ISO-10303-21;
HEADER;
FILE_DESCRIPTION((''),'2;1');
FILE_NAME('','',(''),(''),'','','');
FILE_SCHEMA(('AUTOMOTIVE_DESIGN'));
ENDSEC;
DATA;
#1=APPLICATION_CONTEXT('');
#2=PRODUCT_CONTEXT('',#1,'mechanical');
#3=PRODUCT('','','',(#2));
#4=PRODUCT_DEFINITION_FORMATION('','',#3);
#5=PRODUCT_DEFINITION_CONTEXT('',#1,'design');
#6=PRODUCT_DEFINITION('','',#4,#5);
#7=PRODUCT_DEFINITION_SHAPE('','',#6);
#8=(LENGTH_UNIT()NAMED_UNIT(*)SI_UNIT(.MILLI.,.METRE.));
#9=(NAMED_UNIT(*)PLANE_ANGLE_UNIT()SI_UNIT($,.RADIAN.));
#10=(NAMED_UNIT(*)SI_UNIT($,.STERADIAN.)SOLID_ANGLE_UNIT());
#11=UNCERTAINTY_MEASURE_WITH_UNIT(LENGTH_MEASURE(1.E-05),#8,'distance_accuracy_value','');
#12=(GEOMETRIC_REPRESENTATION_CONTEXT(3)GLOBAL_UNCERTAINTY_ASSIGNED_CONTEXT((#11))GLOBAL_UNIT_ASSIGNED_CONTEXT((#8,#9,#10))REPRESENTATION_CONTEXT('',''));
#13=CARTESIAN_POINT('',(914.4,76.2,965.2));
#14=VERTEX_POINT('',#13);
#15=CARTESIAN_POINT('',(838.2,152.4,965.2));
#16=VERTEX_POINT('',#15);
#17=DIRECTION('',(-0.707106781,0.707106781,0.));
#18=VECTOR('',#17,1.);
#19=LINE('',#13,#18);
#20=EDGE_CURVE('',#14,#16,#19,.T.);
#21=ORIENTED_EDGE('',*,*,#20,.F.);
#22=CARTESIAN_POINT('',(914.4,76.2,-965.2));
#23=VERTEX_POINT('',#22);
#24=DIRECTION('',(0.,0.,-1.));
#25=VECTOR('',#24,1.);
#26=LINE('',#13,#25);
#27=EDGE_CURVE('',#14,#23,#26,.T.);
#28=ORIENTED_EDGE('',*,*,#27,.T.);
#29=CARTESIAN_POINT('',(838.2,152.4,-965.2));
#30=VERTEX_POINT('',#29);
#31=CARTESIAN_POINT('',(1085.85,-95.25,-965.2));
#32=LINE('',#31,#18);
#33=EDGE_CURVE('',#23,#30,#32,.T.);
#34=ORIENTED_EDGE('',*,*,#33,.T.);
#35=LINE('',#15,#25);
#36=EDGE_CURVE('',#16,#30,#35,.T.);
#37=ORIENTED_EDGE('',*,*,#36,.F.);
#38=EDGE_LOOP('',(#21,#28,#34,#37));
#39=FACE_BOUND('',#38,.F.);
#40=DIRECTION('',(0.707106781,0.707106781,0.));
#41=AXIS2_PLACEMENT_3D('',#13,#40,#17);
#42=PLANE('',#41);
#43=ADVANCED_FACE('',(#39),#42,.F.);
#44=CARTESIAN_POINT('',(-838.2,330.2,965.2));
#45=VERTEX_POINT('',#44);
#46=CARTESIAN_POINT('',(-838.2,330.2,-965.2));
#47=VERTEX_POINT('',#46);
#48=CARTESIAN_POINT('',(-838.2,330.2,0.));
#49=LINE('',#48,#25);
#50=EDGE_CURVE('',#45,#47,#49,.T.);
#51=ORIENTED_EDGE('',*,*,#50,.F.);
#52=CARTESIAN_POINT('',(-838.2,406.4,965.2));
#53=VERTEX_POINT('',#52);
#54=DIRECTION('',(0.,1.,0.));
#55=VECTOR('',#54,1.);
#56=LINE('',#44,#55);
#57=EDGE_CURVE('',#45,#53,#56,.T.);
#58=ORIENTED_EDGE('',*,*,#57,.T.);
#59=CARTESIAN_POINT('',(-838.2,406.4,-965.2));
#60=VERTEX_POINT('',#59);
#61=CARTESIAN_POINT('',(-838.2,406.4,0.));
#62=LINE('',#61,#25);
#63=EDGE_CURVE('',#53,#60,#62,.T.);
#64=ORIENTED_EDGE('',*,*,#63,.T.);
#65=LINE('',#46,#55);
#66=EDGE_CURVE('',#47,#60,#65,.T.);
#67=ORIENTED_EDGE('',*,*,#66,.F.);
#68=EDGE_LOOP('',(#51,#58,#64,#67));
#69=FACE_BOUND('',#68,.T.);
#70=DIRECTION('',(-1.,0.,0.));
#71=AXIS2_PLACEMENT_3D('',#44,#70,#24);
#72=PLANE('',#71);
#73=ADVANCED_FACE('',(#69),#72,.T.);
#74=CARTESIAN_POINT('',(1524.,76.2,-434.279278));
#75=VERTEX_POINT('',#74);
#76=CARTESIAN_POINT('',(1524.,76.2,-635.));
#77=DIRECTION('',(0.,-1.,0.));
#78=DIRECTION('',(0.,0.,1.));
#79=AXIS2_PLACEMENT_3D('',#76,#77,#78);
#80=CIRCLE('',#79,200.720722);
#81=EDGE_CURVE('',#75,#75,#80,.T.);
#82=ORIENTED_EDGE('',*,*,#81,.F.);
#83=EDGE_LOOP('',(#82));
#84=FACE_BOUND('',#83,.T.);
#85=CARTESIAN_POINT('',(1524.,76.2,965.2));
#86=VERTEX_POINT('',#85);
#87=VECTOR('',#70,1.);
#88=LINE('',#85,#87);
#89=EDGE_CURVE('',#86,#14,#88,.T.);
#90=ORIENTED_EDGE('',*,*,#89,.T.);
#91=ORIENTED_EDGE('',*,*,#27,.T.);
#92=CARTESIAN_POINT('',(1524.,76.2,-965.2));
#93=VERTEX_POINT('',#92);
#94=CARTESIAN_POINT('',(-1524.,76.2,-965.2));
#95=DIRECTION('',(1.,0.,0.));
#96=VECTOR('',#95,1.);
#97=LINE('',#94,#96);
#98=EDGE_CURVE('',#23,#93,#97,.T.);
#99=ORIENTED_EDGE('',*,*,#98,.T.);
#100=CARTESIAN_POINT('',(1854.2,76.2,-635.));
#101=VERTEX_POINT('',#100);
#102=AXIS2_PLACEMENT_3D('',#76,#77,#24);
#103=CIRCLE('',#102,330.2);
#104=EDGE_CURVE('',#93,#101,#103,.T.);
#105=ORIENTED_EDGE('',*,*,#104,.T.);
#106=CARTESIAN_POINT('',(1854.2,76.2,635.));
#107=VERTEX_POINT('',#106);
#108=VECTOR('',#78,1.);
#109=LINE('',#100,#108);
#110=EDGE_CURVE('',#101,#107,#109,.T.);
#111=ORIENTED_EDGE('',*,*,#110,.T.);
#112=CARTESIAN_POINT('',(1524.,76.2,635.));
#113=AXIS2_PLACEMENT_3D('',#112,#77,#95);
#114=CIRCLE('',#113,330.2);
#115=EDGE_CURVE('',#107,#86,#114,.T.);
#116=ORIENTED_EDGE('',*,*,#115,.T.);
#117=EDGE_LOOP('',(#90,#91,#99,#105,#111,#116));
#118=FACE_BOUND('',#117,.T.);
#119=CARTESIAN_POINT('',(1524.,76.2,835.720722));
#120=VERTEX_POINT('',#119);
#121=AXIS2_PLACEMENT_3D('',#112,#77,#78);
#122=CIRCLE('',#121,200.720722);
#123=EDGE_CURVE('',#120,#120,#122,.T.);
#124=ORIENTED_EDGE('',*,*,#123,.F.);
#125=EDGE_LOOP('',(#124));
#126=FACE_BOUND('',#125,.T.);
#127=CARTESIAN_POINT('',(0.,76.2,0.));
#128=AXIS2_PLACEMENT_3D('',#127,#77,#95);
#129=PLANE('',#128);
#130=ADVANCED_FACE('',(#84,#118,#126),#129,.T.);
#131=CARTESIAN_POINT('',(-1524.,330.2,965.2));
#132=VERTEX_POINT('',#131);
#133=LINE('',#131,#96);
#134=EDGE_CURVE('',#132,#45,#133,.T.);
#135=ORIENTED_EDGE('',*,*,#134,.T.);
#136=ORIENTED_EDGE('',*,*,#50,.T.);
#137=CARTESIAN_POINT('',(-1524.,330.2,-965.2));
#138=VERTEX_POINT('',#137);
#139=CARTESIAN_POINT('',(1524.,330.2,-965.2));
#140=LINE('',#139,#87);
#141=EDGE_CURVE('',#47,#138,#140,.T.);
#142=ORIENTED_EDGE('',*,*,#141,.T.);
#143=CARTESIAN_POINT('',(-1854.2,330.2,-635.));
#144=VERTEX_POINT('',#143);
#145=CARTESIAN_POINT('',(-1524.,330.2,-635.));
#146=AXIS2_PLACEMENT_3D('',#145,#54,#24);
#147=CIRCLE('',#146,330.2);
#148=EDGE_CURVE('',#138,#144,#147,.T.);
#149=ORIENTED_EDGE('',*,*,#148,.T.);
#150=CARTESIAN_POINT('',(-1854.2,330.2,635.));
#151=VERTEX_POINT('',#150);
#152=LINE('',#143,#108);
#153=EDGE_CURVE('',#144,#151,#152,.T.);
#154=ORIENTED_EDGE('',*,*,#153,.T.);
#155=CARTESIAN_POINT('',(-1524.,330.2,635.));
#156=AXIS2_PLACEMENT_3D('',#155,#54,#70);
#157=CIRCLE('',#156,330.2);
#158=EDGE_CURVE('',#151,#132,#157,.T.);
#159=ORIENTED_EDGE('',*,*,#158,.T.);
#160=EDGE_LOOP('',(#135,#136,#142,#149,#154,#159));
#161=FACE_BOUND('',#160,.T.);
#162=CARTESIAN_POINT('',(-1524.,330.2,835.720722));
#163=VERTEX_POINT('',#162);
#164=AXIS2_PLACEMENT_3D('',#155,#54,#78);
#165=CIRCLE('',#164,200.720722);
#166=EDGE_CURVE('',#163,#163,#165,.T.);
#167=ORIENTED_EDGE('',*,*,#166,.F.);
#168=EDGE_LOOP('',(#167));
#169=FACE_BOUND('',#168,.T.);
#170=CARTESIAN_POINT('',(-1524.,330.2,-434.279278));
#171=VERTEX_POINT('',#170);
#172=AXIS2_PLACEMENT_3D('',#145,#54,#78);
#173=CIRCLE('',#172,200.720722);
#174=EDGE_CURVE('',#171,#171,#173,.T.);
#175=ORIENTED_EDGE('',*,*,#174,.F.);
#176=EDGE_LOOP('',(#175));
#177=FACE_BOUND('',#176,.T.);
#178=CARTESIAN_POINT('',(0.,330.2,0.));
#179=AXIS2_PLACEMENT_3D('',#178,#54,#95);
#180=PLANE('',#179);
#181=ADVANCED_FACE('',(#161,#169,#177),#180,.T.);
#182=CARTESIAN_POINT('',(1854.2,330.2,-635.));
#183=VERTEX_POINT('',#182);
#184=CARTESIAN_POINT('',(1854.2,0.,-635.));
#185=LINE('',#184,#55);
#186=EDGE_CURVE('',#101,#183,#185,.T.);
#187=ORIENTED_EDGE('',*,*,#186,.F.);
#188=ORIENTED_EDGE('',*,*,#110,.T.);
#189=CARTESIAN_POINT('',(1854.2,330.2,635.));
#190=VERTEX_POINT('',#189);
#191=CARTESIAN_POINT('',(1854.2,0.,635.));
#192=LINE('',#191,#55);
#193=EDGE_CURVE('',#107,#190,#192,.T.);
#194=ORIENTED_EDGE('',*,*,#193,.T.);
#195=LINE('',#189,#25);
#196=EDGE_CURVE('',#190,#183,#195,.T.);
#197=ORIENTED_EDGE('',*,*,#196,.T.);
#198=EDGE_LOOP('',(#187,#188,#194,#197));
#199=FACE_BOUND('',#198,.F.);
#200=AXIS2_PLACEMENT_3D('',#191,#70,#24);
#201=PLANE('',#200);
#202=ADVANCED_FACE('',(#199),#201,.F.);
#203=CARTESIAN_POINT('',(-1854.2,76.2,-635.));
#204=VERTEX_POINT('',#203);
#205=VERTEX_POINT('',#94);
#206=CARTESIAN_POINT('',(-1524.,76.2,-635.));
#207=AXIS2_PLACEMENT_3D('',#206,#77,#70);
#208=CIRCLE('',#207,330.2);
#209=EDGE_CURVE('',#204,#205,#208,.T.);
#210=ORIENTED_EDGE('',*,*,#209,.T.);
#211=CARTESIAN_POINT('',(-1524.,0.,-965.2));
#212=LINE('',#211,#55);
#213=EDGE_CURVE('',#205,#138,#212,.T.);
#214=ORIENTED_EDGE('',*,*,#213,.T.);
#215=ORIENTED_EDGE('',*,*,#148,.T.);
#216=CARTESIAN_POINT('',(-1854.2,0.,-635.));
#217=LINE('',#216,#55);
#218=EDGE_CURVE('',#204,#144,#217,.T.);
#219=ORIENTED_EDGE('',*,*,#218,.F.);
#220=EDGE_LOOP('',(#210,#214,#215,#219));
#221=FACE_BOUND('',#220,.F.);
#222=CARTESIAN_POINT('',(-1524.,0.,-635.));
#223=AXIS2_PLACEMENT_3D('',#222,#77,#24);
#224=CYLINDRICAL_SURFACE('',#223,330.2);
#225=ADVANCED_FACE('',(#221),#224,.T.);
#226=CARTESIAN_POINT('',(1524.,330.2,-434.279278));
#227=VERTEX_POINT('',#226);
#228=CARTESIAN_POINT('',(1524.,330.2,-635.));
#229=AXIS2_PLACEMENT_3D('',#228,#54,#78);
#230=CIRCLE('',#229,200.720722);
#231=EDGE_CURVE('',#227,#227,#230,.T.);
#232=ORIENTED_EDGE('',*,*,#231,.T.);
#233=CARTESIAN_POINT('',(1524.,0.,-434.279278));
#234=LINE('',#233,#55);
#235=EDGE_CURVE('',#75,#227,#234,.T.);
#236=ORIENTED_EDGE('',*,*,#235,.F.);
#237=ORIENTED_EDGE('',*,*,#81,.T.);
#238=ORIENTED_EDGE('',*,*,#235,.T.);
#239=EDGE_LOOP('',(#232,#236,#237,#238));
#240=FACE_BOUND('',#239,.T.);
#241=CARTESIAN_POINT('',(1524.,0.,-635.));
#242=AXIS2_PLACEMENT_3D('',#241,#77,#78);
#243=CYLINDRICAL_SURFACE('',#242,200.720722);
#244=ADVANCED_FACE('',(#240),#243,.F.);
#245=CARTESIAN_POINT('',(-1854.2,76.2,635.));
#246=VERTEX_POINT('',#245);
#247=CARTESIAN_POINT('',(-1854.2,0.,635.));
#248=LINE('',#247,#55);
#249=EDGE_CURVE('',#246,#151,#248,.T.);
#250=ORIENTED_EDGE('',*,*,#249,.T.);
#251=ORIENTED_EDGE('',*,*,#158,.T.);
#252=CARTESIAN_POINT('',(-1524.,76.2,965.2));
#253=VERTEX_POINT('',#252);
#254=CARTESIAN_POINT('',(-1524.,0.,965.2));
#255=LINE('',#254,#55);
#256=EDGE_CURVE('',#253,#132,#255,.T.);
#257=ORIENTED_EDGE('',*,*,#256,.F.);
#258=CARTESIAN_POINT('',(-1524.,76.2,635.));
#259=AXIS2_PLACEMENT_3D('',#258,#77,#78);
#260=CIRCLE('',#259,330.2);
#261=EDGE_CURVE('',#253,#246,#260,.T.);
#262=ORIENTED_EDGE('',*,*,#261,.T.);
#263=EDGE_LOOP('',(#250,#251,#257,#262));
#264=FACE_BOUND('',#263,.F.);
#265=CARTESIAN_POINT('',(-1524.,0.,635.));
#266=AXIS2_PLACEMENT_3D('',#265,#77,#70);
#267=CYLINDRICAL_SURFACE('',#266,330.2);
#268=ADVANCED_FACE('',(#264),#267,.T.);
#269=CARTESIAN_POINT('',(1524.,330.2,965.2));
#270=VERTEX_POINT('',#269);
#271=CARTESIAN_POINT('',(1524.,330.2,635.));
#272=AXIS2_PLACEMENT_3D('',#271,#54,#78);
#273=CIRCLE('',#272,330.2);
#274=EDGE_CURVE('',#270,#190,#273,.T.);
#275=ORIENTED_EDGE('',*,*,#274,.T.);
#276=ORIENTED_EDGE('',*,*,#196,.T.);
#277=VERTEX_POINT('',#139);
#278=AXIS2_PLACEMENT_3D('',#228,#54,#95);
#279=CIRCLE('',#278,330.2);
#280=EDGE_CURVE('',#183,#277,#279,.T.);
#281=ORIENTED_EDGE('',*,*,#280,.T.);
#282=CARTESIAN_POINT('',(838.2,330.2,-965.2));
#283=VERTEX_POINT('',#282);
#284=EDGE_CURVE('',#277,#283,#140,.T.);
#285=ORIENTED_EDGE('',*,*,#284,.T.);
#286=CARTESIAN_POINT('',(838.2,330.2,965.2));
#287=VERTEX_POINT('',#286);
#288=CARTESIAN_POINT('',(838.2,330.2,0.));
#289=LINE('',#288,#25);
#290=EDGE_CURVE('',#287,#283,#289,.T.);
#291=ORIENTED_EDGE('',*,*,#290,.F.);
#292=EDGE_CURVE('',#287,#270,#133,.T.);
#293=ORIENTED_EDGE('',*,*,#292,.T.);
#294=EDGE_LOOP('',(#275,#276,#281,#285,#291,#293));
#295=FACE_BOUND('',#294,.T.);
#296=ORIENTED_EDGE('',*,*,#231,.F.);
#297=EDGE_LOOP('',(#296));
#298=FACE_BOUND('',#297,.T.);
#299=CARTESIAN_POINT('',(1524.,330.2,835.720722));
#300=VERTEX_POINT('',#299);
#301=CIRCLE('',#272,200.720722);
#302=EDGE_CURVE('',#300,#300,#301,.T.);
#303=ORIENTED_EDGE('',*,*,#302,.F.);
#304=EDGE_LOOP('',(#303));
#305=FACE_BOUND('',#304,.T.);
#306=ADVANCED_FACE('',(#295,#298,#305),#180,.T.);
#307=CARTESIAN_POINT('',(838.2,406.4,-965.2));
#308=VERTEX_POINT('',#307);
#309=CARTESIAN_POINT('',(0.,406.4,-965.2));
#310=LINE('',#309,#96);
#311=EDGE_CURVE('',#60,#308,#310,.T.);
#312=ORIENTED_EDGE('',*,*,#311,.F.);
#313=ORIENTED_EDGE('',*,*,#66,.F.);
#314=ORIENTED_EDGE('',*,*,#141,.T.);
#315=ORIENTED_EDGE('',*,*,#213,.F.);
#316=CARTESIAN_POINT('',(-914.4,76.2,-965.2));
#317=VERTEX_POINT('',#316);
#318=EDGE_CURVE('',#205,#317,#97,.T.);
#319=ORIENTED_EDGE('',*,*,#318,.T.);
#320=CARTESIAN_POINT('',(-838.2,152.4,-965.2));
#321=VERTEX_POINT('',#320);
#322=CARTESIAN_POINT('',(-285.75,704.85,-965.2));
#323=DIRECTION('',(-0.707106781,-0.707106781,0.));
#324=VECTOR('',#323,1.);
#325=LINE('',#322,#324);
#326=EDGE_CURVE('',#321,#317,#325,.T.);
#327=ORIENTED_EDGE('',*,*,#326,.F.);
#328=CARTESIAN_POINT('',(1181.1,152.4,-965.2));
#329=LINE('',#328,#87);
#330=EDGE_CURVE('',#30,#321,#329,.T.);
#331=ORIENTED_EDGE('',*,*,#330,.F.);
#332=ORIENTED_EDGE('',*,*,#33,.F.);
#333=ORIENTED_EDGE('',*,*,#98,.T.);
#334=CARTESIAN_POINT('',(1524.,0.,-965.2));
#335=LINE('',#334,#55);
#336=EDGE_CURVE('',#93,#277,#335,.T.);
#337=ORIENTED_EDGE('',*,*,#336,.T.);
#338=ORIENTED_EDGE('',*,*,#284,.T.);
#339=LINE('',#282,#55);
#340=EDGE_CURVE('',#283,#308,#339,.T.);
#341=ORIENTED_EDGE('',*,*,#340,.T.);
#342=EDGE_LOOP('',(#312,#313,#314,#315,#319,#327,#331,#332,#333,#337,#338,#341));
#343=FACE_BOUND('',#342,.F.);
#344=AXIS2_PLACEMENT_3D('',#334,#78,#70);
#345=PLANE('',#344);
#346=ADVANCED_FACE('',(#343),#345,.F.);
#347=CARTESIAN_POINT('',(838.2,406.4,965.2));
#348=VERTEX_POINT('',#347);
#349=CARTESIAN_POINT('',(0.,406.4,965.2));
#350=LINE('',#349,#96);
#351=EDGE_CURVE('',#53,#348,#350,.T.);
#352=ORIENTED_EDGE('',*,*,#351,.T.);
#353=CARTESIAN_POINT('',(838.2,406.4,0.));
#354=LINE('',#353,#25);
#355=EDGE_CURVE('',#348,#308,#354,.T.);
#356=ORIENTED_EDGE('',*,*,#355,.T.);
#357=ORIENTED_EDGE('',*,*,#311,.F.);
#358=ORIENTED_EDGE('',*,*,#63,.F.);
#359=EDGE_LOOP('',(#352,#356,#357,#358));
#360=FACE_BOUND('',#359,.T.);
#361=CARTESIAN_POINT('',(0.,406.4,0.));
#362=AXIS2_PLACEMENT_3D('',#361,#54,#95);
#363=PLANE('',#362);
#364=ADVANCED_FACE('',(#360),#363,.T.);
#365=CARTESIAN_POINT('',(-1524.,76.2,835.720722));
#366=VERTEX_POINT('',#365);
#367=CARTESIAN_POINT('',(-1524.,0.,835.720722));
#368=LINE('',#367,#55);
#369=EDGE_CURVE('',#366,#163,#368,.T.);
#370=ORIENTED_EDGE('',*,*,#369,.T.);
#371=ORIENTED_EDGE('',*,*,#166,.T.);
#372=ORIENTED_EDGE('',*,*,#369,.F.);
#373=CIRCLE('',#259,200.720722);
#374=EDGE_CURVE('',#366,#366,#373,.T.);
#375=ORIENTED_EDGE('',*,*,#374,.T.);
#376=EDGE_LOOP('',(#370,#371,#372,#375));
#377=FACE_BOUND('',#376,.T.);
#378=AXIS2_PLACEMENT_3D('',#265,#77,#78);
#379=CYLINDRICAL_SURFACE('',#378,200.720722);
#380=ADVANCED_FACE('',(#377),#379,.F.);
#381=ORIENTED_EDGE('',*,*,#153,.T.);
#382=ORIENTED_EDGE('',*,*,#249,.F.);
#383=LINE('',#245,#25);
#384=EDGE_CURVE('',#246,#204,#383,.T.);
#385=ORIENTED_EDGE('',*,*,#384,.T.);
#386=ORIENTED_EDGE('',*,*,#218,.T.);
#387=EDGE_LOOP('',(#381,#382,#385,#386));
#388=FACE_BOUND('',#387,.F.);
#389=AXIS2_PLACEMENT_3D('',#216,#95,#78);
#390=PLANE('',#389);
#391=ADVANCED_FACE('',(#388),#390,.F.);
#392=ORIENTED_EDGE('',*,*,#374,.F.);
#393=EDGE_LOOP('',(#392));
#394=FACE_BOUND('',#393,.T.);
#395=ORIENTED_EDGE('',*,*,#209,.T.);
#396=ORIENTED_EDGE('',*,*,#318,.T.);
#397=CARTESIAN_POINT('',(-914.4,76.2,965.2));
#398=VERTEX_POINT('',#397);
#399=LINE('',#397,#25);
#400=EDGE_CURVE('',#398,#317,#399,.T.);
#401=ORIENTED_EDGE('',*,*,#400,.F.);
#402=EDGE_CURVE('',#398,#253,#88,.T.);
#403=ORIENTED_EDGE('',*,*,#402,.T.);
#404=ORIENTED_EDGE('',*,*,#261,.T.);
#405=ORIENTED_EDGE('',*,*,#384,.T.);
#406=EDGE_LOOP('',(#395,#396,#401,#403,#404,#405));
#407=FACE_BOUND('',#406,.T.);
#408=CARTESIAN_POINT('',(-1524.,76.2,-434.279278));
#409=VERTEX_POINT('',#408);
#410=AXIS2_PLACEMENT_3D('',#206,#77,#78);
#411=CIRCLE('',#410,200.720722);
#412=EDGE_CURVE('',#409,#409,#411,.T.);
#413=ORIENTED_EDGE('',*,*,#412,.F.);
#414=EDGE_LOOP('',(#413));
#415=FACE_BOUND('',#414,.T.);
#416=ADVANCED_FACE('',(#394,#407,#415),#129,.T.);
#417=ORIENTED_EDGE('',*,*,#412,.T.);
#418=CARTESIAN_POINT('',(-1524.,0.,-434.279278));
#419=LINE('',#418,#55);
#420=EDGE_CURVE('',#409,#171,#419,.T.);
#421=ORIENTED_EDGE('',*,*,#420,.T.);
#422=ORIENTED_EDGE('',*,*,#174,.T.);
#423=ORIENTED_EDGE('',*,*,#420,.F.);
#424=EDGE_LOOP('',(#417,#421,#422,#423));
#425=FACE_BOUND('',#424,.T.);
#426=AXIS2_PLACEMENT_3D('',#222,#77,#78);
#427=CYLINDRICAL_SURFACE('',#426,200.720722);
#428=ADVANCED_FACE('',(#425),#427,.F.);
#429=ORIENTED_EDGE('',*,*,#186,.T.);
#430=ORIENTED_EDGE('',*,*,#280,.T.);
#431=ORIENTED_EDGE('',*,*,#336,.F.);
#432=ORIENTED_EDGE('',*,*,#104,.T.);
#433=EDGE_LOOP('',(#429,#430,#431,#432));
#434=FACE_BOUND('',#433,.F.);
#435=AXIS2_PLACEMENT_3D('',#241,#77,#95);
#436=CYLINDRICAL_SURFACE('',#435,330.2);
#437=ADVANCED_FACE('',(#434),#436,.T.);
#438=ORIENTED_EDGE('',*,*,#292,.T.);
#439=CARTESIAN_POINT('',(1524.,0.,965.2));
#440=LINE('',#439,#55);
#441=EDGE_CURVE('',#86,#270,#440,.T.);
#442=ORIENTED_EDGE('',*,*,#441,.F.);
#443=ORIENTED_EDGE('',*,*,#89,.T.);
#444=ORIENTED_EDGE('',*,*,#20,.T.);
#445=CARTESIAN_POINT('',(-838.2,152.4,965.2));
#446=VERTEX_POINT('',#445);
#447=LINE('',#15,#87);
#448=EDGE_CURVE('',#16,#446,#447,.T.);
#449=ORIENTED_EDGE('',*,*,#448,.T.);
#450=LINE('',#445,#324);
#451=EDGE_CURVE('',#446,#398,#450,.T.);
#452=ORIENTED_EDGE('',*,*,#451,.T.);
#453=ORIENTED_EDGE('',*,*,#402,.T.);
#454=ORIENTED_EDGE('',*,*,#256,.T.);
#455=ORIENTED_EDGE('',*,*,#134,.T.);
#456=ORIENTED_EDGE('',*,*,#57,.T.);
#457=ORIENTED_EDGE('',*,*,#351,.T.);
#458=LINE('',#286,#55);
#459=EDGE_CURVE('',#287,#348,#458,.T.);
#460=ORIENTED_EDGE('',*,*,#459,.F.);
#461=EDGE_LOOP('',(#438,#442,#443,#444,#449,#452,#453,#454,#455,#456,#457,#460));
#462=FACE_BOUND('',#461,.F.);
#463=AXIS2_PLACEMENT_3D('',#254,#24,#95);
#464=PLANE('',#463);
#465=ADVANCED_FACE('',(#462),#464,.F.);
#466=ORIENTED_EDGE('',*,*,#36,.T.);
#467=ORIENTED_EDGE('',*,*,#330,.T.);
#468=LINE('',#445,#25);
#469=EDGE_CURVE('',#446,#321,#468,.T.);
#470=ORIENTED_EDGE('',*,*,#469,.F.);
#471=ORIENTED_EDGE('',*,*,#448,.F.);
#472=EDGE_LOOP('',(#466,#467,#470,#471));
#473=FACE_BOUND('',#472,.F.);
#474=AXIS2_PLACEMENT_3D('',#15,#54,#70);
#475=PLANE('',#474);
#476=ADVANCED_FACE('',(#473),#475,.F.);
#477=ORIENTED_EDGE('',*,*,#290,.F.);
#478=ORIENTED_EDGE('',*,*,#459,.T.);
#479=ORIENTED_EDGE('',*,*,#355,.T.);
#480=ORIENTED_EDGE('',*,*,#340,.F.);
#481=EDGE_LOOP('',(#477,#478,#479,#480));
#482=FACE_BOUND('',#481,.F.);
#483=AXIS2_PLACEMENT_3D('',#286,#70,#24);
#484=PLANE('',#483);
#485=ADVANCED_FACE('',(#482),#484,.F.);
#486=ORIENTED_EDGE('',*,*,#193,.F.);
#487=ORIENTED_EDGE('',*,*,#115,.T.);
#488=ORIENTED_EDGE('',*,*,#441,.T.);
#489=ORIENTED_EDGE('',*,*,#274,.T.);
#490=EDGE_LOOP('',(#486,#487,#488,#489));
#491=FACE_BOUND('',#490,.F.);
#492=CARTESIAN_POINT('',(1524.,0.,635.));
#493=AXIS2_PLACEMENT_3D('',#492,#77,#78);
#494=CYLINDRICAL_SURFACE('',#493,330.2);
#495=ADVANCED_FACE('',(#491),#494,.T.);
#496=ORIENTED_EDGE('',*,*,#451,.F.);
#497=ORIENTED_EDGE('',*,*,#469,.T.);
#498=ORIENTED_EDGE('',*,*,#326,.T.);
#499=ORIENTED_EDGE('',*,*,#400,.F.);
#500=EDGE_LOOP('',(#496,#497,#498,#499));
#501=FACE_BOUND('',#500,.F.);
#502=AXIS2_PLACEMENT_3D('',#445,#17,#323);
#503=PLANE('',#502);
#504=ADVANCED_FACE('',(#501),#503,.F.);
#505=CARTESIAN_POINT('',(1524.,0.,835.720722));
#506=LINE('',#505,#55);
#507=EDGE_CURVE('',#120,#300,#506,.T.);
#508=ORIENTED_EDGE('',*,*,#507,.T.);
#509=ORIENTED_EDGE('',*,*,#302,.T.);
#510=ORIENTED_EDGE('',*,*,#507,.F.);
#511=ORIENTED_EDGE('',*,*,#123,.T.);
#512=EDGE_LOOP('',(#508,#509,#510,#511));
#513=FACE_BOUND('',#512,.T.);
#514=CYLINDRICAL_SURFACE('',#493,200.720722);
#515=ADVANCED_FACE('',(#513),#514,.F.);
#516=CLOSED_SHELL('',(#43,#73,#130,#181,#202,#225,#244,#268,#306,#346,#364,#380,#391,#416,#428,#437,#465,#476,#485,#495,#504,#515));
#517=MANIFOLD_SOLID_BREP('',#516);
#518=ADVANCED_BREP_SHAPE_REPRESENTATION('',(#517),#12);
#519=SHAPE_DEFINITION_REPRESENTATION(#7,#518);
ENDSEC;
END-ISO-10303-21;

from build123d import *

# Parameters (mm, degrees)
SKETCH1_R           = 200.720721903
BOSS_EXTRUDE1_DEPTH = 330.2
SKETCH3_W           = 1676.4
SKETCH3_H           = 1930.4
BOSS_EXTRUDE4_DEPTH = 76.2
CUT_EXTRUDE2_DEPTH  = 76.2
CUT_EXTRUDE6_DEPTH  = 2708.334992202


with BuildPart() as part:
    # Sketch1 → Boss-Extrude1 (new body)
    with BuildSketch(Plane(origin=(0, 0, 0), x_dir=(1, 0, 0), z_dir=(0, 1, 0))):
        with BuildLine():
            Line((1524, 965.2), (-1524, 965.2))
            ThreePointArc((-1524, 965.2), (-1757.486659148, 868.486659148), (-1854.2, 635))
            Line((-1854.2, 635), (-1854.2, -635))
            ThreePointArc((-1854.2, -635), (-1757.486659148, -868.486659148), (-1524, -965.2))
            Line((-1524, -965.2), (1524, -965.2))
            ThreePointArc((1524, -965.2), (1757.486659148, -868.486659148), (1854.2, -635))
            Line((1854.2, -635), (1854.2, 635))
            ThreePointArc((1854.2, 635), (1757.486659148, 868.486659148), (1524, 965.2))
        make_face()
        with Locations(Location((-1524, 635, 0), (0, 0, 270))):
            Circle(SKETCH1_R, mode=Mode.SUBTRACT)
        with Locations(Location((1524, 635, 0), (0, 0, 270))):
            Circle(SKETCH1_R, mode=Mode.SUBTRACT)
        with Locations(Location((1524, -635, 0), (0, 0, 270))):
            Circle(SKETCH1_R, mode=Mode.SUBTRACT)
        with Locations(Location((-1524, -635, 0), (0, 0, 270))):
            Circle(SKETCH1_R, mode=Mode.SUBTRACT)
    extrude(amount=BOSS_EXTRUDE1_DEPTH)

    # Sketch3 → Boss-Extrude4 (add)
    with BuildSketch(Plane(origin=(0, 330.2, 0), x_dir=(1, 0, 0), z_dir=(0, 1, 0))):
        Rectangle(SKETCH3_W, SKETCH3_H)
    extrude(amount=BOSS_EXTRUDE4_DEPTH)

    # Sketch5 → Cut-Extrude2 (cut)
    with BuildSketch(Plane.XZ):
        with BuildLine():
            Line((-1524, -965.2), (1524, -965.2))
            ThreePointArc((1524, -965.2), (1757.486659148, -868.486659148), (1854.2, -635))
            Line((1854.2, -635), (1854.2, 635))
            ThreePointArc((1854.2, 635), (1757.486659148, 868.486659148), (1524, 965.2))
            Line((1524, 965.2), (-1524, 965.2))
            ThreePointArc((-1524, 965.2), (-1757.486659148, 868.486659148), (-1854.2, 635))
            Line((-1854.2, 635), (-1854.2, -635))
            ThreePointArc((-1854.2, -635), (-1757.486659148, -868.486659148), (-1524, -965.2))
        make_face()
    extrude(amount=-CUT_EXTRUDE2_DEPTH, mode=Mode.SUBTRACT)

    # Sketch6 → Cut-Extrude6 (cut, through all)
    with BuildSketch(Plane.XY.offset(965.2)):
        Polygon((-914.4, 76.2), (914.4, 76.2), (838.2, 152.4), (-838.2, 152.4), align=None)
    extrude(amount=-CUT_EXTRUDE6_DEPTH, mode=Mode.SUBTRACT)


solid = part.part
